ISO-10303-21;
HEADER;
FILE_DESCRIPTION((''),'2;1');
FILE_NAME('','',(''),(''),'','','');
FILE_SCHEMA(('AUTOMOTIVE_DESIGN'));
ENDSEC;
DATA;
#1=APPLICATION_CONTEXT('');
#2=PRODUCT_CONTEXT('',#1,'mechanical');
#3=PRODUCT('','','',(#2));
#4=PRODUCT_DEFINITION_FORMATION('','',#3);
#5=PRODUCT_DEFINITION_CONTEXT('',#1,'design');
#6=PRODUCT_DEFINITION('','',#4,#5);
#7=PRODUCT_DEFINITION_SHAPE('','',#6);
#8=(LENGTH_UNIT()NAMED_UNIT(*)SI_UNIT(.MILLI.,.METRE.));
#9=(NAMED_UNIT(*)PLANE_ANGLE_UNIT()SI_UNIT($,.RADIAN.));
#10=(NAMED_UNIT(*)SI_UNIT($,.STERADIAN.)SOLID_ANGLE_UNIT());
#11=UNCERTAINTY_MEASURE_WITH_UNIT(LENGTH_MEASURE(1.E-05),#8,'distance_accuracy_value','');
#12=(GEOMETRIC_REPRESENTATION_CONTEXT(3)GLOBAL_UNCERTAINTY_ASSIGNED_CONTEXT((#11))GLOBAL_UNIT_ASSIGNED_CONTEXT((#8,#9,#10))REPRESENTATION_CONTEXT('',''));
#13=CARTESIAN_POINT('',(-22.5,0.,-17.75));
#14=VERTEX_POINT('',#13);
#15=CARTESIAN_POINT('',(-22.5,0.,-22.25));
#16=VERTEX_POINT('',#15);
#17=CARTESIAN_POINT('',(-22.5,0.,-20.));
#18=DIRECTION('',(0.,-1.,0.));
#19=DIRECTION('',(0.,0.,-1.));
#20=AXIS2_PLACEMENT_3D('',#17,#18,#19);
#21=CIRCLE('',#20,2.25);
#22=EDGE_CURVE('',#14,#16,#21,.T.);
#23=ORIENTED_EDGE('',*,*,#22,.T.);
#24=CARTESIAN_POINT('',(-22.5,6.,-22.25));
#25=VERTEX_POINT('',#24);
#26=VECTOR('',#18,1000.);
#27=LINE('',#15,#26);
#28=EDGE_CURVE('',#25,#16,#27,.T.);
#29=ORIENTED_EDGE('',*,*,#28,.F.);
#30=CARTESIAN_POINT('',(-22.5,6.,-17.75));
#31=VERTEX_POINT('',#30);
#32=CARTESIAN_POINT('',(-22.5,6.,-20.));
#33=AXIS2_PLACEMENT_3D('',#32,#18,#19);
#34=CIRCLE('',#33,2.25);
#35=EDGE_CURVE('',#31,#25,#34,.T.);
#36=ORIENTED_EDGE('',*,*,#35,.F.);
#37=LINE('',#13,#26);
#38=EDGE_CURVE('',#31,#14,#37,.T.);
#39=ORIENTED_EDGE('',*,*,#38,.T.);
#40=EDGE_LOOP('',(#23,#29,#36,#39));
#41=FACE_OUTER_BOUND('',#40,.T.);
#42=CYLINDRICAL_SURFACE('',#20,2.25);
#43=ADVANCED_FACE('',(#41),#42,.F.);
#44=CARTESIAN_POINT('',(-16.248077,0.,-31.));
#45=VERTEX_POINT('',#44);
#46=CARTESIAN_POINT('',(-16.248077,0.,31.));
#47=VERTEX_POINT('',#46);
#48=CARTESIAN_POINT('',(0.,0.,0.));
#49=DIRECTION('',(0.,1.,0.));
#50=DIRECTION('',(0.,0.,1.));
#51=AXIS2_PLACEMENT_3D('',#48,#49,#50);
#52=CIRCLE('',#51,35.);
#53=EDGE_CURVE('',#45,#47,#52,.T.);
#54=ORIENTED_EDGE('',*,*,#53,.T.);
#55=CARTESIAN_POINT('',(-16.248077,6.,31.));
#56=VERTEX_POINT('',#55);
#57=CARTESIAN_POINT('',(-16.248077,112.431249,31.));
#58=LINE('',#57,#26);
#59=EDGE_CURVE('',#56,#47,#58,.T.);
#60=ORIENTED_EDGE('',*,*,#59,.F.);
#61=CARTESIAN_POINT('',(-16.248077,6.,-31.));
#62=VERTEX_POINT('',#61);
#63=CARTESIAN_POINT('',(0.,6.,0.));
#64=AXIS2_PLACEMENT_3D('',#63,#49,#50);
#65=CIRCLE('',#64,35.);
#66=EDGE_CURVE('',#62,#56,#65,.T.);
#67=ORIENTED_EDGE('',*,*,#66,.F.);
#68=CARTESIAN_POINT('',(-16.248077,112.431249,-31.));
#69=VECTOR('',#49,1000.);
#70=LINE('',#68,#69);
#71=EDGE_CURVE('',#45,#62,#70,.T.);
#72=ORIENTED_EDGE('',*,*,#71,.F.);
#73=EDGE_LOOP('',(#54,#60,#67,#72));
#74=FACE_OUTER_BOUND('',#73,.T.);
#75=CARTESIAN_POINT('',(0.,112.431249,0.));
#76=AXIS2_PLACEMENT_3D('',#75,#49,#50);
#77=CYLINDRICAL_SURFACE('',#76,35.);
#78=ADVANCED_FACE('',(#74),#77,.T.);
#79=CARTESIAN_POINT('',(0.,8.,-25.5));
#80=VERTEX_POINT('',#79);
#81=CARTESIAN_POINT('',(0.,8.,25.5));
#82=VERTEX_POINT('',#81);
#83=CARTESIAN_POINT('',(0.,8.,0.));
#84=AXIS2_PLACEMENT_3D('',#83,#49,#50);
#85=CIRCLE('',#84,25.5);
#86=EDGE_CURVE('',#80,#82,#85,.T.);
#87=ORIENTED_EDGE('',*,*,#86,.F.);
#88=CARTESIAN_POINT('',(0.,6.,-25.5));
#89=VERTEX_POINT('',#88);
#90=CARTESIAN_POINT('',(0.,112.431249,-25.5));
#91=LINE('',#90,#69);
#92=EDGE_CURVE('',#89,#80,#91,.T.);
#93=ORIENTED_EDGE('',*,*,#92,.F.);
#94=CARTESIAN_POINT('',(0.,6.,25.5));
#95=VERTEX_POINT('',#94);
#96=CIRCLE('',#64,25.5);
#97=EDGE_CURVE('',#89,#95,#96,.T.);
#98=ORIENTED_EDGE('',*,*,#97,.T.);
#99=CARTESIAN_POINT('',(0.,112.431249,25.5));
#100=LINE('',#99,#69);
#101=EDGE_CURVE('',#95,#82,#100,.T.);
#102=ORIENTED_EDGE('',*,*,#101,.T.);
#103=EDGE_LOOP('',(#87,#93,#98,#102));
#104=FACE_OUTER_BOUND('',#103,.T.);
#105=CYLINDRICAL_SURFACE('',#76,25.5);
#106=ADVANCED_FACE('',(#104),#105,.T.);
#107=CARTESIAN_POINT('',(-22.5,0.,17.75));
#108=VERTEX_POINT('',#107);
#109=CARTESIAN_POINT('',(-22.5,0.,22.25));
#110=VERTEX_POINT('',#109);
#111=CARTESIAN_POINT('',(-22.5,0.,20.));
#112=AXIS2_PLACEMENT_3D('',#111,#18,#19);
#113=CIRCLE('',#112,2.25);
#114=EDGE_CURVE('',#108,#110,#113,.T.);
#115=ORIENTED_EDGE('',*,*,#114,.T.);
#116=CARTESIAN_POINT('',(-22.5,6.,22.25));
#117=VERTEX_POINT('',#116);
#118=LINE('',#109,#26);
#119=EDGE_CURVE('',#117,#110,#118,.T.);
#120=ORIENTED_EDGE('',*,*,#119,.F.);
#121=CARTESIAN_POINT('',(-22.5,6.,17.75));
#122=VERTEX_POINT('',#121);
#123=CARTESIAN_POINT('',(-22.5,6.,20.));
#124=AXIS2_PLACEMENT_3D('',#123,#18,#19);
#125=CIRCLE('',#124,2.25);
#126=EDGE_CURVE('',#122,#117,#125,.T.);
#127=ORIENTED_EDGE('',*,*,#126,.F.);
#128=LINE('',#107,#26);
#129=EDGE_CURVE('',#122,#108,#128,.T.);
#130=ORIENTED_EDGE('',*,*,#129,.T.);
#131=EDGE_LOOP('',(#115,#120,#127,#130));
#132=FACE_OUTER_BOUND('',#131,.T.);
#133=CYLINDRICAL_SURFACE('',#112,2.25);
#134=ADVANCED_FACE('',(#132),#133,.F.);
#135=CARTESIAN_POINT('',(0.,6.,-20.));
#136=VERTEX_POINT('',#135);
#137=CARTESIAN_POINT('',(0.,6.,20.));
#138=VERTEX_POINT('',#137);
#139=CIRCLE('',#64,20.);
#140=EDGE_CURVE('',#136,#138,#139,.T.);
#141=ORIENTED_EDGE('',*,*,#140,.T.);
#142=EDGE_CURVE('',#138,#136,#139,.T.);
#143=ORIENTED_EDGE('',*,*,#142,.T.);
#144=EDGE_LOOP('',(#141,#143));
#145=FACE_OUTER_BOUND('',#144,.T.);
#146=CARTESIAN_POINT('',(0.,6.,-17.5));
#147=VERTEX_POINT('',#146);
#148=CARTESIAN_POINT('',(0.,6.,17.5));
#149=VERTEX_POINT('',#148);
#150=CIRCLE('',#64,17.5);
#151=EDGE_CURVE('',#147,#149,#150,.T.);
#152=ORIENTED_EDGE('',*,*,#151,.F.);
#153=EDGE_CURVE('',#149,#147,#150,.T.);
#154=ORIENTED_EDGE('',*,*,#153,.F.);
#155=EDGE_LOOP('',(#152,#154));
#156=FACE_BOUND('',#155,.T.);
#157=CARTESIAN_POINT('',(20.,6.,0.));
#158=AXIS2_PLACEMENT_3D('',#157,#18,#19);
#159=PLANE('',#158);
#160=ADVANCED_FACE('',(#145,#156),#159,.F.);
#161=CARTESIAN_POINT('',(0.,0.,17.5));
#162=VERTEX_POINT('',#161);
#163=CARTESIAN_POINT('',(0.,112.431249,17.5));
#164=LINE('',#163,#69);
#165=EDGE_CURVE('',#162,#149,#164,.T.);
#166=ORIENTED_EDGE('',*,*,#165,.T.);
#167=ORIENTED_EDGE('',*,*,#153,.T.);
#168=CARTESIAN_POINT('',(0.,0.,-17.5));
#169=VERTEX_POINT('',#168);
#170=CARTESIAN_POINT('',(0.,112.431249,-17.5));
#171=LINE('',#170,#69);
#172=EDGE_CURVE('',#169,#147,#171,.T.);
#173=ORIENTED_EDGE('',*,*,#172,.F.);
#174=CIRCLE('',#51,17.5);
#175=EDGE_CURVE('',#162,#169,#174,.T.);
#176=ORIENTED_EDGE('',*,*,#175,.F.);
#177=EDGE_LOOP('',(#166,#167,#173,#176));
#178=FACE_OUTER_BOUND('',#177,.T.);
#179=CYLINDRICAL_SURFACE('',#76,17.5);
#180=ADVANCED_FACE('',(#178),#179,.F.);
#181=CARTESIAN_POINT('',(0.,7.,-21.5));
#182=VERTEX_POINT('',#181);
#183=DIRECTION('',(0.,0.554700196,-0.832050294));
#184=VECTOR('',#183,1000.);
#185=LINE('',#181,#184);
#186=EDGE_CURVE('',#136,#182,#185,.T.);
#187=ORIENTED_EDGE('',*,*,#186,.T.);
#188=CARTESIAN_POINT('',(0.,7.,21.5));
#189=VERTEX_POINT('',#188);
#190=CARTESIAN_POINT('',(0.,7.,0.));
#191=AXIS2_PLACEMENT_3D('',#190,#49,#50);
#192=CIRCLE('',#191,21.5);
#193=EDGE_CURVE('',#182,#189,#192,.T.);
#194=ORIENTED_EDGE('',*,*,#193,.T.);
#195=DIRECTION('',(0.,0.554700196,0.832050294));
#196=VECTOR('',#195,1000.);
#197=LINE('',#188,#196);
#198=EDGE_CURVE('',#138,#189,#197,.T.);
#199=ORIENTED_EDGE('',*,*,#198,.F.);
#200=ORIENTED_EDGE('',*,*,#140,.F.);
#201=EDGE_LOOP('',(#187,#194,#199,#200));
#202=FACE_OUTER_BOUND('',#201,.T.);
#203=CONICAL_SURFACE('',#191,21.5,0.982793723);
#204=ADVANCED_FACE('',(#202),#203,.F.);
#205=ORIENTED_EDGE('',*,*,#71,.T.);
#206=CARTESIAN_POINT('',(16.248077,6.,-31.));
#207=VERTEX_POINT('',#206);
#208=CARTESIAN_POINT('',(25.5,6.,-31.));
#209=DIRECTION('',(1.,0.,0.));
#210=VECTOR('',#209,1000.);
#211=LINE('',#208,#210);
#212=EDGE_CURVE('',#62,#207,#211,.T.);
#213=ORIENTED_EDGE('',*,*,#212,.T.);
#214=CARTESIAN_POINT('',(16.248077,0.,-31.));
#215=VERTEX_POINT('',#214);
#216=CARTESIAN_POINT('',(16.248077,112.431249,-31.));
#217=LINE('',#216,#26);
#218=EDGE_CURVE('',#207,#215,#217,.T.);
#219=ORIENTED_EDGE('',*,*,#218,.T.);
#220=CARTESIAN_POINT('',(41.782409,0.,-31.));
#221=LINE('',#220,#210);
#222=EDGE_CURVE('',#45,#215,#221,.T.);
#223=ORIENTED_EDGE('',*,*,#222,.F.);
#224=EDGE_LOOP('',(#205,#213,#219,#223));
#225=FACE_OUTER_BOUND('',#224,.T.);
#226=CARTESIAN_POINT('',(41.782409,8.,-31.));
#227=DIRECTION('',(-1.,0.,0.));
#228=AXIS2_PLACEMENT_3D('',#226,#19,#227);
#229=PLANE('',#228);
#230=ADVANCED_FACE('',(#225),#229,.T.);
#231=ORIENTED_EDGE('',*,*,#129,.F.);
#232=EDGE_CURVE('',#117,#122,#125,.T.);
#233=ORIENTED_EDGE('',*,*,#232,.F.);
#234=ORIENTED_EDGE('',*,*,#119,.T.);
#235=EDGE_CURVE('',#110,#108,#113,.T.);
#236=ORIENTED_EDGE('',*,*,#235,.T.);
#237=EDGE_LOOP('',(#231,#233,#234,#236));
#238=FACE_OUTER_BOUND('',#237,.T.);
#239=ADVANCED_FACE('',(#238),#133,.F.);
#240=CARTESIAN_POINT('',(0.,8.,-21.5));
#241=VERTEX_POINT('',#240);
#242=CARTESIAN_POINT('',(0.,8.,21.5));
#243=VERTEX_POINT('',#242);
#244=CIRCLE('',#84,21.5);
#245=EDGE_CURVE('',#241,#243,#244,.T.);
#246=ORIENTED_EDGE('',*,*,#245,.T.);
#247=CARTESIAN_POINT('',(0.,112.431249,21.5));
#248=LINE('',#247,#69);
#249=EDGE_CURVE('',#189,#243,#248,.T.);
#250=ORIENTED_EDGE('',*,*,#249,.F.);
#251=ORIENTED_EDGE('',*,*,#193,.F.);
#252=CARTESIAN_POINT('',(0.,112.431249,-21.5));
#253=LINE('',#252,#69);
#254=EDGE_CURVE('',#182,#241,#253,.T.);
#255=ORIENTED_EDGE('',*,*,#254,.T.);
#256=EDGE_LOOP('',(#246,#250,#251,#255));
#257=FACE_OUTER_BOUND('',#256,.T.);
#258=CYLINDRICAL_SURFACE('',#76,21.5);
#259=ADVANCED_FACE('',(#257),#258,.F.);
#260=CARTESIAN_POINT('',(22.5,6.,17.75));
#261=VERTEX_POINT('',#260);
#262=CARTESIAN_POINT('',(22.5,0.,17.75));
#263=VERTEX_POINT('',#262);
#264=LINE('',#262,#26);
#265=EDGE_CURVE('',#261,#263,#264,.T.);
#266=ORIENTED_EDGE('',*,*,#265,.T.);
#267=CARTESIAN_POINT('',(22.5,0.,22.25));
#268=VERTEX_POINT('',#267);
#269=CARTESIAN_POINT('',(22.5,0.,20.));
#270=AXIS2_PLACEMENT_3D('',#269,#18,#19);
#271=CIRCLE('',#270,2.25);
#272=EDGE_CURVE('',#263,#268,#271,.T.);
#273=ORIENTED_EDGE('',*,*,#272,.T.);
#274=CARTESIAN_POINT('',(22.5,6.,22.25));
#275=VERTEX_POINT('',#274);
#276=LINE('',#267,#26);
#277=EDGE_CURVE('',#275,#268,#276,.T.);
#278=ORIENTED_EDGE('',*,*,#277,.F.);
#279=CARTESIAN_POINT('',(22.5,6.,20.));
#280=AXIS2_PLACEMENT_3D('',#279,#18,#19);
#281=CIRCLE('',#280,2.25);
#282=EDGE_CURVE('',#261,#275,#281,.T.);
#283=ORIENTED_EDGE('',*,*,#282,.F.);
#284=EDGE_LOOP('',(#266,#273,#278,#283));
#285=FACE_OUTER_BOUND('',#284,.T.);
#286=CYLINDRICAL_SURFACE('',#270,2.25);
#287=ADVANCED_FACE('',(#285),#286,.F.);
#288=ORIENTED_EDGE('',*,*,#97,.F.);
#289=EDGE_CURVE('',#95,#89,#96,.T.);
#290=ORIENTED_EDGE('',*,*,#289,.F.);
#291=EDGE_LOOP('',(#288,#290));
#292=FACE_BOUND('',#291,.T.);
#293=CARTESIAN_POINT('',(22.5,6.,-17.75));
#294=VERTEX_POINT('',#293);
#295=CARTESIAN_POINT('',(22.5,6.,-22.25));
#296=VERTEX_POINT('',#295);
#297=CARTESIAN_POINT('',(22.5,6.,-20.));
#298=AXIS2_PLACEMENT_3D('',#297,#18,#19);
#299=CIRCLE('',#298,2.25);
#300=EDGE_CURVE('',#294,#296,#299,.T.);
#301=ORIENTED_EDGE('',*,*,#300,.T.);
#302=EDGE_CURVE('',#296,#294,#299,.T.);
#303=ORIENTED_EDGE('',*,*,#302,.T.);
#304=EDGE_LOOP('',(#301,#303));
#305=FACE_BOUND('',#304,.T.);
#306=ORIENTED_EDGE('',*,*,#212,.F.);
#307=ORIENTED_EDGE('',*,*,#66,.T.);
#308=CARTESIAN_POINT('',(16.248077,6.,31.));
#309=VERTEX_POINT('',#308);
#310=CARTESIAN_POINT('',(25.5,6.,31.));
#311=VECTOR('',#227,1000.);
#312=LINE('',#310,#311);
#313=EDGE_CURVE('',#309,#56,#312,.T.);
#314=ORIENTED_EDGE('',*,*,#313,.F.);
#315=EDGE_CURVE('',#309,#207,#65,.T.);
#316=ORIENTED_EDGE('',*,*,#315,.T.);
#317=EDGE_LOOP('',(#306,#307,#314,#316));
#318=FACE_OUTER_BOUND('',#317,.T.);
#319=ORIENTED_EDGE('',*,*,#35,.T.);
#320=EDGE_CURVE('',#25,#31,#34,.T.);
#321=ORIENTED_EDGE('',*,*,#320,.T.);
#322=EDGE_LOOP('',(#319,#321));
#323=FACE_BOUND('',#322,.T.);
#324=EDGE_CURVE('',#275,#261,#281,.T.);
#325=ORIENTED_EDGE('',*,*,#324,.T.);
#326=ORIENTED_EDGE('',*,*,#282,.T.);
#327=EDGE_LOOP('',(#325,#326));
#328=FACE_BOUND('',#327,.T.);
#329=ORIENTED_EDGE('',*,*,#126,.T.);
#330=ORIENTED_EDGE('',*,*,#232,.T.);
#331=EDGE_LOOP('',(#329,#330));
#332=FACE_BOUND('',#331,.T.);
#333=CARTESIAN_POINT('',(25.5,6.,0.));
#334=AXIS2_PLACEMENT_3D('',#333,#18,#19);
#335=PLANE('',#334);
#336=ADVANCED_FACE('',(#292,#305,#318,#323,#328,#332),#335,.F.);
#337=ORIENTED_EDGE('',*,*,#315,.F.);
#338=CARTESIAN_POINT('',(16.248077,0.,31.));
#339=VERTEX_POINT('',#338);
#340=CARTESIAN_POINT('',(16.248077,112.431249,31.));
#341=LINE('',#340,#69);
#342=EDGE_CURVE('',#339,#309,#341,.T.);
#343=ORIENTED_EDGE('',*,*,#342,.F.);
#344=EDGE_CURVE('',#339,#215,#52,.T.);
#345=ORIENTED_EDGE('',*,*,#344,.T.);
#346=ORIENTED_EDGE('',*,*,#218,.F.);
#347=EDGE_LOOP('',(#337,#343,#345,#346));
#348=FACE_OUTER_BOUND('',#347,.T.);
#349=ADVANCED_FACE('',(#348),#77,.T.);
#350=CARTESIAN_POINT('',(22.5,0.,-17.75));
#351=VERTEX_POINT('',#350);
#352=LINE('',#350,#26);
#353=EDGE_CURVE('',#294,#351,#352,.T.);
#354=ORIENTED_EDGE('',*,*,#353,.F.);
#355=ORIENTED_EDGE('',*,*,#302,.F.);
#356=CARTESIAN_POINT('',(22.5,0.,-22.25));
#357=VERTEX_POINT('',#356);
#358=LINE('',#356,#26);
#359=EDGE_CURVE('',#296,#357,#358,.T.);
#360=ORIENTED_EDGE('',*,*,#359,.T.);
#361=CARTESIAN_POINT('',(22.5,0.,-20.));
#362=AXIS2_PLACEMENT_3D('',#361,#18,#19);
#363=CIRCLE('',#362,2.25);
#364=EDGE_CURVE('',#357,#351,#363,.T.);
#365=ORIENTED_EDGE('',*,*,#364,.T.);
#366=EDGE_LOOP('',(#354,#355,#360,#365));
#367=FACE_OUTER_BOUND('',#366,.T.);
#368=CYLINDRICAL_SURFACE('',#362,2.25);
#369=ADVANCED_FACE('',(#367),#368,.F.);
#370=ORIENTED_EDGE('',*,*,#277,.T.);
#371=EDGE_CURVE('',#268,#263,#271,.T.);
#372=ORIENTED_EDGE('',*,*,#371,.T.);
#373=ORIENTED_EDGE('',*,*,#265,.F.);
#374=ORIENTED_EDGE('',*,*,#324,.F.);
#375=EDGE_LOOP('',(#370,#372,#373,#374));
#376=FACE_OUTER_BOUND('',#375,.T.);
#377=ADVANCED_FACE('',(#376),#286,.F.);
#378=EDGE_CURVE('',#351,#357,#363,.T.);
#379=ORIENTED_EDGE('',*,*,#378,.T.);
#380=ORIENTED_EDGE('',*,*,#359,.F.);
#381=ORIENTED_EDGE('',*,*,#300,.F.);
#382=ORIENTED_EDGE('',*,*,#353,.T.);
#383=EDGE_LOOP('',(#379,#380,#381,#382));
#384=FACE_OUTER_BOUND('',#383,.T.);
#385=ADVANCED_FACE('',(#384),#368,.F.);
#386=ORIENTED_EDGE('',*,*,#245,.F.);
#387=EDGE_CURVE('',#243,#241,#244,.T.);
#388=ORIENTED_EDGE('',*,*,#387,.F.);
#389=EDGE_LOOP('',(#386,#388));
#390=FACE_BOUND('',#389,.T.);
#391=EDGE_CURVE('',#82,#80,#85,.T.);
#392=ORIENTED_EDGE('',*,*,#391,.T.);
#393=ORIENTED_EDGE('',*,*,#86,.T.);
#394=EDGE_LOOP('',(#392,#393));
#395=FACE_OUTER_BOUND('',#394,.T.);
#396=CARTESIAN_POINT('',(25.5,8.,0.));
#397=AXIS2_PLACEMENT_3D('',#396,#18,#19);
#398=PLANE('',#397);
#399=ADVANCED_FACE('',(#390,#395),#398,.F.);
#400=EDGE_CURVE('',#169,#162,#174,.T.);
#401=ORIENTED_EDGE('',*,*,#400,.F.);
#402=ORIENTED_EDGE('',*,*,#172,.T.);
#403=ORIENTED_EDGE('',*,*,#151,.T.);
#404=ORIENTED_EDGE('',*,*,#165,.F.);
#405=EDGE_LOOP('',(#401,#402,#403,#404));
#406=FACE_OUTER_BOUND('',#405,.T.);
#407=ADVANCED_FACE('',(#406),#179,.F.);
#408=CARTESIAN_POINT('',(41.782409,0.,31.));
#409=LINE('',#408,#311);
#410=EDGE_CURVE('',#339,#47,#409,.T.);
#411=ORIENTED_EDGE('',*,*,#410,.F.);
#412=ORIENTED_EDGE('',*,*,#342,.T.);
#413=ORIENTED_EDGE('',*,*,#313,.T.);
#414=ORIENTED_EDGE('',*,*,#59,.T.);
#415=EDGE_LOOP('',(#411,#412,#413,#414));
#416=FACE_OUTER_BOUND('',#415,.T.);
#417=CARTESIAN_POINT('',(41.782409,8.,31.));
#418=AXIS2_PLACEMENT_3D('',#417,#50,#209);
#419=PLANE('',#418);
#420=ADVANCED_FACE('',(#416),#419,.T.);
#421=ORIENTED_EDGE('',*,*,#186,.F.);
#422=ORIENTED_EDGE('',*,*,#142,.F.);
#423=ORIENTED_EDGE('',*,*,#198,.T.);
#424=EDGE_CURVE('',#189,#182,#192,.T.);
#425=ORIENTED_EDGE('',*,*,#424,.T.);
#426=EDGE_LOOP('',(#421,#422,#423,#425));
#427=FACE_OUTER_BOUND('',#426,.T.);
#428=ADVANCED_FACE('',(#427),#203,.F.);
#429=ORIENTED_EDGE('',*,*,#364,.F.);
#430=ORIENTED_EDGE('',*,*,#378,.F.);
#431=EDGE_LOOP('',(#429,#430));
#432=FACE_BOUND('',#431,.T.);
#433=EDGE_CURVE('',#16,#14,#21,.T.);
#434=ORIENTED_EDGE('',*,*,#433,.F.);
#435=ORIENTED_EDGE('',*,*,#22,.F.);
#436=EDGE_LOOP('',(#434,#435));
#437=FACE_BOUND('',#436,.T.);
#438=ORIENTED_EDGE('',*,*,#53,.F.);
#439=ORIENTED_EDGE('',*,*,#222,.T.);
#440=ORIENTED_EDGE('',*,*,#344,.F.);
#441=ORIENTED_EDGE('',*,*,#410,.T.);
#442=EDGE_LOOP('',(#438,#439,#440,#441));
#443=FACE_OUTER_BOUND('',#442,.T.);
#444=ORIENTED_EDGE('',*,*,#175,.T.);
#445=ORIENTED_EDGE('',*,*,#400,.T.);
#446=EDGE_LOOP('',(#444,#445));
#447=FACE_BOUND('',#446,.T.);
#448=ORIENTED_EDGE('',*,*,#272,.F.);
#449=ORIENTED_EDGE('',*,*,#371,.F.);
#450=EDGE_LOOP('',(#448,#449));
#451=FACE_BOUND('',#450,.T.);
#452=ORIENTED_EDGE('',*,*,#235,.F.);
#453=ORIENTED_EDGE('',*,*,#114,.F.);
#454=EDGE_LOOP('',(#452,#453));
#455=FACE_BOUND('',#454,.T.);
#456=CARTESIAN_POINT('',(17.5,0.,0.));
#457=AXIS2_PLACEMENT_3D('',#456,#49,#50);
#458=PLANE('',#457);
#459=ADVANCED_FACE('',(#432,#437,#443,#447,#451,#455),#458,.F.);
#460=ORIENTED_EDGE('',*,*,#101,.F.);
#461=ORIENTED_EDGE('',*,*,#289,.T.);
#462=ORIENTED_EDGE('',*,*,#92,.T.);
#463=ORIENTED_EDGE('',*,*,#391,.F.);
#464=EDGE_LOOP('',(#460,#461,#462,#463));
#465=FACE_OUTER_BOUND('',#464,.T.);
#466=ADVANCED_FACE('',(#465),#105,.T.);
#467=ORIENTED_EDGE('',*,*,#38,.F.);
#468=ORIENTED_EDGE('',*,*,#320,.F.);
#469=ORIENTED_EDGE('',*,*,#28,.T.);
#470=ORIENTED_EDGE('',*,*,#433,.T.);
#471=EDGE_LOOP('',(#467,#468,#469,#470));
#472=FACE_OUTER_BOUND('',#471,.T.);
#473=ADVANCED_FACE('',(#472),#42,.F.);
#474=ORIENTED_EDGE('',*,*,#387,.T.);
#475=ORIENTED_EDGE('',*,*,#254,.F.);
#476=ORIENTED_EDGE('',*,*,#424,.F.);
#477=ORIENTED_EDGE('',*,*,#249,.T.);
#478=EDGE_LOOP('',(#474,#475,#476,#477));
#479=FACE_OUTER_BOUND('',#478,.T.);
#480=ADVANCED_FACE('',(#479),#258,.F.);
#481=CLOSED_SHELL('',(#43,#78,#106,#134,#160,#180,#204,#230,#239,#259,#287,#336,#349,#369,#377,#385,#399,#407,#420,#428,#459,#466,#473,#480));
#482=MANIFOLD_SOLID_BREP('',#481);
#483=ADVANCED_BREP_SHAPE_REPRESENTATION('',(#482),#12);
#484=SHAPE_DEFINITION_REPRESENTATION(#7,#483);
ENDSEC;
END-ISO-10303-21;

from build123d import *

# Parameters (mm, degrees)
F_4_5_4_5_DIAMETER_HOLE1_D     = 4.5
F_4_5_4_5_DIAMETER_HOLE1_DEPTH = 18
F_4_5_4_5_DIAMETER_HOLE1_TIP   = 1.351936393
SKETCH4_OUTSIDE_W              = 91.864
SKETCH4_OUTSIDE_H              = 91.864
SKETCH4_OUTSIDE_W_2            = 83.56481814
SKETCH4_OUTSIDE_H_2            = 62
CUT_EXTRUDE1_DEPTH             = 51.139804547


with BuildPart() as part:
    # Sketch1 → Revolve1 (revolve)
    with BuildSketch(Plane.XY, mode=Mode.PRIVATE) as revolve1_sk:
        Polygon((17.5, 0), (35, 0), (35, 6), (25.5, 6), (25.5, 8), (21.5, 8), (21.5, 7), (20, 6), (17.5, 6), align=None)
    revolve(revolve1_sk.sketch.rotate(Axis((0, 112.43124941, 0), (0, -1, 0)), 90), axis=Axis((0, 112.43124941, 0), (0, -1, 0)))

    # Ø4.5 (4.5) Diameter Hole1
    with Locations(Plane(origin=(0, 0, 0), x_dir=(-1, 0, 0), z_dir=(0, -1, 0))):
        with Locations((-22.5, 20), (-22.5, -20), (22.5, 20), (22.5, -20)):
            Hole(F_4_5_4_5_DIAMETER_HOLE1_D / 2, depth=F_4_5_4_5_DIAMETER_HOLE1_DEPTH)
            with Locations((0, 0, -(F_4_5_4_5_DIAMETER_HOLE1_DEPTH + F_4_5_4_5_DIAMETER_HOLE1_TIP / 2))):  # 118° drill point
                Cone(0, F_4_5_4_5_DIAMETER_HOLE1_D / 2, F_4_5_4_5_DIAMETER_HOLE1_TIP, mode=Mode.SUBTRACT)

    # Sketch4 outside → Cut-Extrude1 (cut, through all)
    with BuildSketch(Plane.XZ):
        Rectangle(SKETCH4_OUTSIDE_W, SKETCH4_OUTSIDE_H)
        Rectangle(SKETCH4_OUTSIDE_W_2, SKETCH4_OUTSIDE_H_2, mode=Mode.SUBTRACT)
    extrude(amount=-CUT_EXTRUDE1_DEPTH, mode=Mode.SUBTRACT)


solid = part.part
